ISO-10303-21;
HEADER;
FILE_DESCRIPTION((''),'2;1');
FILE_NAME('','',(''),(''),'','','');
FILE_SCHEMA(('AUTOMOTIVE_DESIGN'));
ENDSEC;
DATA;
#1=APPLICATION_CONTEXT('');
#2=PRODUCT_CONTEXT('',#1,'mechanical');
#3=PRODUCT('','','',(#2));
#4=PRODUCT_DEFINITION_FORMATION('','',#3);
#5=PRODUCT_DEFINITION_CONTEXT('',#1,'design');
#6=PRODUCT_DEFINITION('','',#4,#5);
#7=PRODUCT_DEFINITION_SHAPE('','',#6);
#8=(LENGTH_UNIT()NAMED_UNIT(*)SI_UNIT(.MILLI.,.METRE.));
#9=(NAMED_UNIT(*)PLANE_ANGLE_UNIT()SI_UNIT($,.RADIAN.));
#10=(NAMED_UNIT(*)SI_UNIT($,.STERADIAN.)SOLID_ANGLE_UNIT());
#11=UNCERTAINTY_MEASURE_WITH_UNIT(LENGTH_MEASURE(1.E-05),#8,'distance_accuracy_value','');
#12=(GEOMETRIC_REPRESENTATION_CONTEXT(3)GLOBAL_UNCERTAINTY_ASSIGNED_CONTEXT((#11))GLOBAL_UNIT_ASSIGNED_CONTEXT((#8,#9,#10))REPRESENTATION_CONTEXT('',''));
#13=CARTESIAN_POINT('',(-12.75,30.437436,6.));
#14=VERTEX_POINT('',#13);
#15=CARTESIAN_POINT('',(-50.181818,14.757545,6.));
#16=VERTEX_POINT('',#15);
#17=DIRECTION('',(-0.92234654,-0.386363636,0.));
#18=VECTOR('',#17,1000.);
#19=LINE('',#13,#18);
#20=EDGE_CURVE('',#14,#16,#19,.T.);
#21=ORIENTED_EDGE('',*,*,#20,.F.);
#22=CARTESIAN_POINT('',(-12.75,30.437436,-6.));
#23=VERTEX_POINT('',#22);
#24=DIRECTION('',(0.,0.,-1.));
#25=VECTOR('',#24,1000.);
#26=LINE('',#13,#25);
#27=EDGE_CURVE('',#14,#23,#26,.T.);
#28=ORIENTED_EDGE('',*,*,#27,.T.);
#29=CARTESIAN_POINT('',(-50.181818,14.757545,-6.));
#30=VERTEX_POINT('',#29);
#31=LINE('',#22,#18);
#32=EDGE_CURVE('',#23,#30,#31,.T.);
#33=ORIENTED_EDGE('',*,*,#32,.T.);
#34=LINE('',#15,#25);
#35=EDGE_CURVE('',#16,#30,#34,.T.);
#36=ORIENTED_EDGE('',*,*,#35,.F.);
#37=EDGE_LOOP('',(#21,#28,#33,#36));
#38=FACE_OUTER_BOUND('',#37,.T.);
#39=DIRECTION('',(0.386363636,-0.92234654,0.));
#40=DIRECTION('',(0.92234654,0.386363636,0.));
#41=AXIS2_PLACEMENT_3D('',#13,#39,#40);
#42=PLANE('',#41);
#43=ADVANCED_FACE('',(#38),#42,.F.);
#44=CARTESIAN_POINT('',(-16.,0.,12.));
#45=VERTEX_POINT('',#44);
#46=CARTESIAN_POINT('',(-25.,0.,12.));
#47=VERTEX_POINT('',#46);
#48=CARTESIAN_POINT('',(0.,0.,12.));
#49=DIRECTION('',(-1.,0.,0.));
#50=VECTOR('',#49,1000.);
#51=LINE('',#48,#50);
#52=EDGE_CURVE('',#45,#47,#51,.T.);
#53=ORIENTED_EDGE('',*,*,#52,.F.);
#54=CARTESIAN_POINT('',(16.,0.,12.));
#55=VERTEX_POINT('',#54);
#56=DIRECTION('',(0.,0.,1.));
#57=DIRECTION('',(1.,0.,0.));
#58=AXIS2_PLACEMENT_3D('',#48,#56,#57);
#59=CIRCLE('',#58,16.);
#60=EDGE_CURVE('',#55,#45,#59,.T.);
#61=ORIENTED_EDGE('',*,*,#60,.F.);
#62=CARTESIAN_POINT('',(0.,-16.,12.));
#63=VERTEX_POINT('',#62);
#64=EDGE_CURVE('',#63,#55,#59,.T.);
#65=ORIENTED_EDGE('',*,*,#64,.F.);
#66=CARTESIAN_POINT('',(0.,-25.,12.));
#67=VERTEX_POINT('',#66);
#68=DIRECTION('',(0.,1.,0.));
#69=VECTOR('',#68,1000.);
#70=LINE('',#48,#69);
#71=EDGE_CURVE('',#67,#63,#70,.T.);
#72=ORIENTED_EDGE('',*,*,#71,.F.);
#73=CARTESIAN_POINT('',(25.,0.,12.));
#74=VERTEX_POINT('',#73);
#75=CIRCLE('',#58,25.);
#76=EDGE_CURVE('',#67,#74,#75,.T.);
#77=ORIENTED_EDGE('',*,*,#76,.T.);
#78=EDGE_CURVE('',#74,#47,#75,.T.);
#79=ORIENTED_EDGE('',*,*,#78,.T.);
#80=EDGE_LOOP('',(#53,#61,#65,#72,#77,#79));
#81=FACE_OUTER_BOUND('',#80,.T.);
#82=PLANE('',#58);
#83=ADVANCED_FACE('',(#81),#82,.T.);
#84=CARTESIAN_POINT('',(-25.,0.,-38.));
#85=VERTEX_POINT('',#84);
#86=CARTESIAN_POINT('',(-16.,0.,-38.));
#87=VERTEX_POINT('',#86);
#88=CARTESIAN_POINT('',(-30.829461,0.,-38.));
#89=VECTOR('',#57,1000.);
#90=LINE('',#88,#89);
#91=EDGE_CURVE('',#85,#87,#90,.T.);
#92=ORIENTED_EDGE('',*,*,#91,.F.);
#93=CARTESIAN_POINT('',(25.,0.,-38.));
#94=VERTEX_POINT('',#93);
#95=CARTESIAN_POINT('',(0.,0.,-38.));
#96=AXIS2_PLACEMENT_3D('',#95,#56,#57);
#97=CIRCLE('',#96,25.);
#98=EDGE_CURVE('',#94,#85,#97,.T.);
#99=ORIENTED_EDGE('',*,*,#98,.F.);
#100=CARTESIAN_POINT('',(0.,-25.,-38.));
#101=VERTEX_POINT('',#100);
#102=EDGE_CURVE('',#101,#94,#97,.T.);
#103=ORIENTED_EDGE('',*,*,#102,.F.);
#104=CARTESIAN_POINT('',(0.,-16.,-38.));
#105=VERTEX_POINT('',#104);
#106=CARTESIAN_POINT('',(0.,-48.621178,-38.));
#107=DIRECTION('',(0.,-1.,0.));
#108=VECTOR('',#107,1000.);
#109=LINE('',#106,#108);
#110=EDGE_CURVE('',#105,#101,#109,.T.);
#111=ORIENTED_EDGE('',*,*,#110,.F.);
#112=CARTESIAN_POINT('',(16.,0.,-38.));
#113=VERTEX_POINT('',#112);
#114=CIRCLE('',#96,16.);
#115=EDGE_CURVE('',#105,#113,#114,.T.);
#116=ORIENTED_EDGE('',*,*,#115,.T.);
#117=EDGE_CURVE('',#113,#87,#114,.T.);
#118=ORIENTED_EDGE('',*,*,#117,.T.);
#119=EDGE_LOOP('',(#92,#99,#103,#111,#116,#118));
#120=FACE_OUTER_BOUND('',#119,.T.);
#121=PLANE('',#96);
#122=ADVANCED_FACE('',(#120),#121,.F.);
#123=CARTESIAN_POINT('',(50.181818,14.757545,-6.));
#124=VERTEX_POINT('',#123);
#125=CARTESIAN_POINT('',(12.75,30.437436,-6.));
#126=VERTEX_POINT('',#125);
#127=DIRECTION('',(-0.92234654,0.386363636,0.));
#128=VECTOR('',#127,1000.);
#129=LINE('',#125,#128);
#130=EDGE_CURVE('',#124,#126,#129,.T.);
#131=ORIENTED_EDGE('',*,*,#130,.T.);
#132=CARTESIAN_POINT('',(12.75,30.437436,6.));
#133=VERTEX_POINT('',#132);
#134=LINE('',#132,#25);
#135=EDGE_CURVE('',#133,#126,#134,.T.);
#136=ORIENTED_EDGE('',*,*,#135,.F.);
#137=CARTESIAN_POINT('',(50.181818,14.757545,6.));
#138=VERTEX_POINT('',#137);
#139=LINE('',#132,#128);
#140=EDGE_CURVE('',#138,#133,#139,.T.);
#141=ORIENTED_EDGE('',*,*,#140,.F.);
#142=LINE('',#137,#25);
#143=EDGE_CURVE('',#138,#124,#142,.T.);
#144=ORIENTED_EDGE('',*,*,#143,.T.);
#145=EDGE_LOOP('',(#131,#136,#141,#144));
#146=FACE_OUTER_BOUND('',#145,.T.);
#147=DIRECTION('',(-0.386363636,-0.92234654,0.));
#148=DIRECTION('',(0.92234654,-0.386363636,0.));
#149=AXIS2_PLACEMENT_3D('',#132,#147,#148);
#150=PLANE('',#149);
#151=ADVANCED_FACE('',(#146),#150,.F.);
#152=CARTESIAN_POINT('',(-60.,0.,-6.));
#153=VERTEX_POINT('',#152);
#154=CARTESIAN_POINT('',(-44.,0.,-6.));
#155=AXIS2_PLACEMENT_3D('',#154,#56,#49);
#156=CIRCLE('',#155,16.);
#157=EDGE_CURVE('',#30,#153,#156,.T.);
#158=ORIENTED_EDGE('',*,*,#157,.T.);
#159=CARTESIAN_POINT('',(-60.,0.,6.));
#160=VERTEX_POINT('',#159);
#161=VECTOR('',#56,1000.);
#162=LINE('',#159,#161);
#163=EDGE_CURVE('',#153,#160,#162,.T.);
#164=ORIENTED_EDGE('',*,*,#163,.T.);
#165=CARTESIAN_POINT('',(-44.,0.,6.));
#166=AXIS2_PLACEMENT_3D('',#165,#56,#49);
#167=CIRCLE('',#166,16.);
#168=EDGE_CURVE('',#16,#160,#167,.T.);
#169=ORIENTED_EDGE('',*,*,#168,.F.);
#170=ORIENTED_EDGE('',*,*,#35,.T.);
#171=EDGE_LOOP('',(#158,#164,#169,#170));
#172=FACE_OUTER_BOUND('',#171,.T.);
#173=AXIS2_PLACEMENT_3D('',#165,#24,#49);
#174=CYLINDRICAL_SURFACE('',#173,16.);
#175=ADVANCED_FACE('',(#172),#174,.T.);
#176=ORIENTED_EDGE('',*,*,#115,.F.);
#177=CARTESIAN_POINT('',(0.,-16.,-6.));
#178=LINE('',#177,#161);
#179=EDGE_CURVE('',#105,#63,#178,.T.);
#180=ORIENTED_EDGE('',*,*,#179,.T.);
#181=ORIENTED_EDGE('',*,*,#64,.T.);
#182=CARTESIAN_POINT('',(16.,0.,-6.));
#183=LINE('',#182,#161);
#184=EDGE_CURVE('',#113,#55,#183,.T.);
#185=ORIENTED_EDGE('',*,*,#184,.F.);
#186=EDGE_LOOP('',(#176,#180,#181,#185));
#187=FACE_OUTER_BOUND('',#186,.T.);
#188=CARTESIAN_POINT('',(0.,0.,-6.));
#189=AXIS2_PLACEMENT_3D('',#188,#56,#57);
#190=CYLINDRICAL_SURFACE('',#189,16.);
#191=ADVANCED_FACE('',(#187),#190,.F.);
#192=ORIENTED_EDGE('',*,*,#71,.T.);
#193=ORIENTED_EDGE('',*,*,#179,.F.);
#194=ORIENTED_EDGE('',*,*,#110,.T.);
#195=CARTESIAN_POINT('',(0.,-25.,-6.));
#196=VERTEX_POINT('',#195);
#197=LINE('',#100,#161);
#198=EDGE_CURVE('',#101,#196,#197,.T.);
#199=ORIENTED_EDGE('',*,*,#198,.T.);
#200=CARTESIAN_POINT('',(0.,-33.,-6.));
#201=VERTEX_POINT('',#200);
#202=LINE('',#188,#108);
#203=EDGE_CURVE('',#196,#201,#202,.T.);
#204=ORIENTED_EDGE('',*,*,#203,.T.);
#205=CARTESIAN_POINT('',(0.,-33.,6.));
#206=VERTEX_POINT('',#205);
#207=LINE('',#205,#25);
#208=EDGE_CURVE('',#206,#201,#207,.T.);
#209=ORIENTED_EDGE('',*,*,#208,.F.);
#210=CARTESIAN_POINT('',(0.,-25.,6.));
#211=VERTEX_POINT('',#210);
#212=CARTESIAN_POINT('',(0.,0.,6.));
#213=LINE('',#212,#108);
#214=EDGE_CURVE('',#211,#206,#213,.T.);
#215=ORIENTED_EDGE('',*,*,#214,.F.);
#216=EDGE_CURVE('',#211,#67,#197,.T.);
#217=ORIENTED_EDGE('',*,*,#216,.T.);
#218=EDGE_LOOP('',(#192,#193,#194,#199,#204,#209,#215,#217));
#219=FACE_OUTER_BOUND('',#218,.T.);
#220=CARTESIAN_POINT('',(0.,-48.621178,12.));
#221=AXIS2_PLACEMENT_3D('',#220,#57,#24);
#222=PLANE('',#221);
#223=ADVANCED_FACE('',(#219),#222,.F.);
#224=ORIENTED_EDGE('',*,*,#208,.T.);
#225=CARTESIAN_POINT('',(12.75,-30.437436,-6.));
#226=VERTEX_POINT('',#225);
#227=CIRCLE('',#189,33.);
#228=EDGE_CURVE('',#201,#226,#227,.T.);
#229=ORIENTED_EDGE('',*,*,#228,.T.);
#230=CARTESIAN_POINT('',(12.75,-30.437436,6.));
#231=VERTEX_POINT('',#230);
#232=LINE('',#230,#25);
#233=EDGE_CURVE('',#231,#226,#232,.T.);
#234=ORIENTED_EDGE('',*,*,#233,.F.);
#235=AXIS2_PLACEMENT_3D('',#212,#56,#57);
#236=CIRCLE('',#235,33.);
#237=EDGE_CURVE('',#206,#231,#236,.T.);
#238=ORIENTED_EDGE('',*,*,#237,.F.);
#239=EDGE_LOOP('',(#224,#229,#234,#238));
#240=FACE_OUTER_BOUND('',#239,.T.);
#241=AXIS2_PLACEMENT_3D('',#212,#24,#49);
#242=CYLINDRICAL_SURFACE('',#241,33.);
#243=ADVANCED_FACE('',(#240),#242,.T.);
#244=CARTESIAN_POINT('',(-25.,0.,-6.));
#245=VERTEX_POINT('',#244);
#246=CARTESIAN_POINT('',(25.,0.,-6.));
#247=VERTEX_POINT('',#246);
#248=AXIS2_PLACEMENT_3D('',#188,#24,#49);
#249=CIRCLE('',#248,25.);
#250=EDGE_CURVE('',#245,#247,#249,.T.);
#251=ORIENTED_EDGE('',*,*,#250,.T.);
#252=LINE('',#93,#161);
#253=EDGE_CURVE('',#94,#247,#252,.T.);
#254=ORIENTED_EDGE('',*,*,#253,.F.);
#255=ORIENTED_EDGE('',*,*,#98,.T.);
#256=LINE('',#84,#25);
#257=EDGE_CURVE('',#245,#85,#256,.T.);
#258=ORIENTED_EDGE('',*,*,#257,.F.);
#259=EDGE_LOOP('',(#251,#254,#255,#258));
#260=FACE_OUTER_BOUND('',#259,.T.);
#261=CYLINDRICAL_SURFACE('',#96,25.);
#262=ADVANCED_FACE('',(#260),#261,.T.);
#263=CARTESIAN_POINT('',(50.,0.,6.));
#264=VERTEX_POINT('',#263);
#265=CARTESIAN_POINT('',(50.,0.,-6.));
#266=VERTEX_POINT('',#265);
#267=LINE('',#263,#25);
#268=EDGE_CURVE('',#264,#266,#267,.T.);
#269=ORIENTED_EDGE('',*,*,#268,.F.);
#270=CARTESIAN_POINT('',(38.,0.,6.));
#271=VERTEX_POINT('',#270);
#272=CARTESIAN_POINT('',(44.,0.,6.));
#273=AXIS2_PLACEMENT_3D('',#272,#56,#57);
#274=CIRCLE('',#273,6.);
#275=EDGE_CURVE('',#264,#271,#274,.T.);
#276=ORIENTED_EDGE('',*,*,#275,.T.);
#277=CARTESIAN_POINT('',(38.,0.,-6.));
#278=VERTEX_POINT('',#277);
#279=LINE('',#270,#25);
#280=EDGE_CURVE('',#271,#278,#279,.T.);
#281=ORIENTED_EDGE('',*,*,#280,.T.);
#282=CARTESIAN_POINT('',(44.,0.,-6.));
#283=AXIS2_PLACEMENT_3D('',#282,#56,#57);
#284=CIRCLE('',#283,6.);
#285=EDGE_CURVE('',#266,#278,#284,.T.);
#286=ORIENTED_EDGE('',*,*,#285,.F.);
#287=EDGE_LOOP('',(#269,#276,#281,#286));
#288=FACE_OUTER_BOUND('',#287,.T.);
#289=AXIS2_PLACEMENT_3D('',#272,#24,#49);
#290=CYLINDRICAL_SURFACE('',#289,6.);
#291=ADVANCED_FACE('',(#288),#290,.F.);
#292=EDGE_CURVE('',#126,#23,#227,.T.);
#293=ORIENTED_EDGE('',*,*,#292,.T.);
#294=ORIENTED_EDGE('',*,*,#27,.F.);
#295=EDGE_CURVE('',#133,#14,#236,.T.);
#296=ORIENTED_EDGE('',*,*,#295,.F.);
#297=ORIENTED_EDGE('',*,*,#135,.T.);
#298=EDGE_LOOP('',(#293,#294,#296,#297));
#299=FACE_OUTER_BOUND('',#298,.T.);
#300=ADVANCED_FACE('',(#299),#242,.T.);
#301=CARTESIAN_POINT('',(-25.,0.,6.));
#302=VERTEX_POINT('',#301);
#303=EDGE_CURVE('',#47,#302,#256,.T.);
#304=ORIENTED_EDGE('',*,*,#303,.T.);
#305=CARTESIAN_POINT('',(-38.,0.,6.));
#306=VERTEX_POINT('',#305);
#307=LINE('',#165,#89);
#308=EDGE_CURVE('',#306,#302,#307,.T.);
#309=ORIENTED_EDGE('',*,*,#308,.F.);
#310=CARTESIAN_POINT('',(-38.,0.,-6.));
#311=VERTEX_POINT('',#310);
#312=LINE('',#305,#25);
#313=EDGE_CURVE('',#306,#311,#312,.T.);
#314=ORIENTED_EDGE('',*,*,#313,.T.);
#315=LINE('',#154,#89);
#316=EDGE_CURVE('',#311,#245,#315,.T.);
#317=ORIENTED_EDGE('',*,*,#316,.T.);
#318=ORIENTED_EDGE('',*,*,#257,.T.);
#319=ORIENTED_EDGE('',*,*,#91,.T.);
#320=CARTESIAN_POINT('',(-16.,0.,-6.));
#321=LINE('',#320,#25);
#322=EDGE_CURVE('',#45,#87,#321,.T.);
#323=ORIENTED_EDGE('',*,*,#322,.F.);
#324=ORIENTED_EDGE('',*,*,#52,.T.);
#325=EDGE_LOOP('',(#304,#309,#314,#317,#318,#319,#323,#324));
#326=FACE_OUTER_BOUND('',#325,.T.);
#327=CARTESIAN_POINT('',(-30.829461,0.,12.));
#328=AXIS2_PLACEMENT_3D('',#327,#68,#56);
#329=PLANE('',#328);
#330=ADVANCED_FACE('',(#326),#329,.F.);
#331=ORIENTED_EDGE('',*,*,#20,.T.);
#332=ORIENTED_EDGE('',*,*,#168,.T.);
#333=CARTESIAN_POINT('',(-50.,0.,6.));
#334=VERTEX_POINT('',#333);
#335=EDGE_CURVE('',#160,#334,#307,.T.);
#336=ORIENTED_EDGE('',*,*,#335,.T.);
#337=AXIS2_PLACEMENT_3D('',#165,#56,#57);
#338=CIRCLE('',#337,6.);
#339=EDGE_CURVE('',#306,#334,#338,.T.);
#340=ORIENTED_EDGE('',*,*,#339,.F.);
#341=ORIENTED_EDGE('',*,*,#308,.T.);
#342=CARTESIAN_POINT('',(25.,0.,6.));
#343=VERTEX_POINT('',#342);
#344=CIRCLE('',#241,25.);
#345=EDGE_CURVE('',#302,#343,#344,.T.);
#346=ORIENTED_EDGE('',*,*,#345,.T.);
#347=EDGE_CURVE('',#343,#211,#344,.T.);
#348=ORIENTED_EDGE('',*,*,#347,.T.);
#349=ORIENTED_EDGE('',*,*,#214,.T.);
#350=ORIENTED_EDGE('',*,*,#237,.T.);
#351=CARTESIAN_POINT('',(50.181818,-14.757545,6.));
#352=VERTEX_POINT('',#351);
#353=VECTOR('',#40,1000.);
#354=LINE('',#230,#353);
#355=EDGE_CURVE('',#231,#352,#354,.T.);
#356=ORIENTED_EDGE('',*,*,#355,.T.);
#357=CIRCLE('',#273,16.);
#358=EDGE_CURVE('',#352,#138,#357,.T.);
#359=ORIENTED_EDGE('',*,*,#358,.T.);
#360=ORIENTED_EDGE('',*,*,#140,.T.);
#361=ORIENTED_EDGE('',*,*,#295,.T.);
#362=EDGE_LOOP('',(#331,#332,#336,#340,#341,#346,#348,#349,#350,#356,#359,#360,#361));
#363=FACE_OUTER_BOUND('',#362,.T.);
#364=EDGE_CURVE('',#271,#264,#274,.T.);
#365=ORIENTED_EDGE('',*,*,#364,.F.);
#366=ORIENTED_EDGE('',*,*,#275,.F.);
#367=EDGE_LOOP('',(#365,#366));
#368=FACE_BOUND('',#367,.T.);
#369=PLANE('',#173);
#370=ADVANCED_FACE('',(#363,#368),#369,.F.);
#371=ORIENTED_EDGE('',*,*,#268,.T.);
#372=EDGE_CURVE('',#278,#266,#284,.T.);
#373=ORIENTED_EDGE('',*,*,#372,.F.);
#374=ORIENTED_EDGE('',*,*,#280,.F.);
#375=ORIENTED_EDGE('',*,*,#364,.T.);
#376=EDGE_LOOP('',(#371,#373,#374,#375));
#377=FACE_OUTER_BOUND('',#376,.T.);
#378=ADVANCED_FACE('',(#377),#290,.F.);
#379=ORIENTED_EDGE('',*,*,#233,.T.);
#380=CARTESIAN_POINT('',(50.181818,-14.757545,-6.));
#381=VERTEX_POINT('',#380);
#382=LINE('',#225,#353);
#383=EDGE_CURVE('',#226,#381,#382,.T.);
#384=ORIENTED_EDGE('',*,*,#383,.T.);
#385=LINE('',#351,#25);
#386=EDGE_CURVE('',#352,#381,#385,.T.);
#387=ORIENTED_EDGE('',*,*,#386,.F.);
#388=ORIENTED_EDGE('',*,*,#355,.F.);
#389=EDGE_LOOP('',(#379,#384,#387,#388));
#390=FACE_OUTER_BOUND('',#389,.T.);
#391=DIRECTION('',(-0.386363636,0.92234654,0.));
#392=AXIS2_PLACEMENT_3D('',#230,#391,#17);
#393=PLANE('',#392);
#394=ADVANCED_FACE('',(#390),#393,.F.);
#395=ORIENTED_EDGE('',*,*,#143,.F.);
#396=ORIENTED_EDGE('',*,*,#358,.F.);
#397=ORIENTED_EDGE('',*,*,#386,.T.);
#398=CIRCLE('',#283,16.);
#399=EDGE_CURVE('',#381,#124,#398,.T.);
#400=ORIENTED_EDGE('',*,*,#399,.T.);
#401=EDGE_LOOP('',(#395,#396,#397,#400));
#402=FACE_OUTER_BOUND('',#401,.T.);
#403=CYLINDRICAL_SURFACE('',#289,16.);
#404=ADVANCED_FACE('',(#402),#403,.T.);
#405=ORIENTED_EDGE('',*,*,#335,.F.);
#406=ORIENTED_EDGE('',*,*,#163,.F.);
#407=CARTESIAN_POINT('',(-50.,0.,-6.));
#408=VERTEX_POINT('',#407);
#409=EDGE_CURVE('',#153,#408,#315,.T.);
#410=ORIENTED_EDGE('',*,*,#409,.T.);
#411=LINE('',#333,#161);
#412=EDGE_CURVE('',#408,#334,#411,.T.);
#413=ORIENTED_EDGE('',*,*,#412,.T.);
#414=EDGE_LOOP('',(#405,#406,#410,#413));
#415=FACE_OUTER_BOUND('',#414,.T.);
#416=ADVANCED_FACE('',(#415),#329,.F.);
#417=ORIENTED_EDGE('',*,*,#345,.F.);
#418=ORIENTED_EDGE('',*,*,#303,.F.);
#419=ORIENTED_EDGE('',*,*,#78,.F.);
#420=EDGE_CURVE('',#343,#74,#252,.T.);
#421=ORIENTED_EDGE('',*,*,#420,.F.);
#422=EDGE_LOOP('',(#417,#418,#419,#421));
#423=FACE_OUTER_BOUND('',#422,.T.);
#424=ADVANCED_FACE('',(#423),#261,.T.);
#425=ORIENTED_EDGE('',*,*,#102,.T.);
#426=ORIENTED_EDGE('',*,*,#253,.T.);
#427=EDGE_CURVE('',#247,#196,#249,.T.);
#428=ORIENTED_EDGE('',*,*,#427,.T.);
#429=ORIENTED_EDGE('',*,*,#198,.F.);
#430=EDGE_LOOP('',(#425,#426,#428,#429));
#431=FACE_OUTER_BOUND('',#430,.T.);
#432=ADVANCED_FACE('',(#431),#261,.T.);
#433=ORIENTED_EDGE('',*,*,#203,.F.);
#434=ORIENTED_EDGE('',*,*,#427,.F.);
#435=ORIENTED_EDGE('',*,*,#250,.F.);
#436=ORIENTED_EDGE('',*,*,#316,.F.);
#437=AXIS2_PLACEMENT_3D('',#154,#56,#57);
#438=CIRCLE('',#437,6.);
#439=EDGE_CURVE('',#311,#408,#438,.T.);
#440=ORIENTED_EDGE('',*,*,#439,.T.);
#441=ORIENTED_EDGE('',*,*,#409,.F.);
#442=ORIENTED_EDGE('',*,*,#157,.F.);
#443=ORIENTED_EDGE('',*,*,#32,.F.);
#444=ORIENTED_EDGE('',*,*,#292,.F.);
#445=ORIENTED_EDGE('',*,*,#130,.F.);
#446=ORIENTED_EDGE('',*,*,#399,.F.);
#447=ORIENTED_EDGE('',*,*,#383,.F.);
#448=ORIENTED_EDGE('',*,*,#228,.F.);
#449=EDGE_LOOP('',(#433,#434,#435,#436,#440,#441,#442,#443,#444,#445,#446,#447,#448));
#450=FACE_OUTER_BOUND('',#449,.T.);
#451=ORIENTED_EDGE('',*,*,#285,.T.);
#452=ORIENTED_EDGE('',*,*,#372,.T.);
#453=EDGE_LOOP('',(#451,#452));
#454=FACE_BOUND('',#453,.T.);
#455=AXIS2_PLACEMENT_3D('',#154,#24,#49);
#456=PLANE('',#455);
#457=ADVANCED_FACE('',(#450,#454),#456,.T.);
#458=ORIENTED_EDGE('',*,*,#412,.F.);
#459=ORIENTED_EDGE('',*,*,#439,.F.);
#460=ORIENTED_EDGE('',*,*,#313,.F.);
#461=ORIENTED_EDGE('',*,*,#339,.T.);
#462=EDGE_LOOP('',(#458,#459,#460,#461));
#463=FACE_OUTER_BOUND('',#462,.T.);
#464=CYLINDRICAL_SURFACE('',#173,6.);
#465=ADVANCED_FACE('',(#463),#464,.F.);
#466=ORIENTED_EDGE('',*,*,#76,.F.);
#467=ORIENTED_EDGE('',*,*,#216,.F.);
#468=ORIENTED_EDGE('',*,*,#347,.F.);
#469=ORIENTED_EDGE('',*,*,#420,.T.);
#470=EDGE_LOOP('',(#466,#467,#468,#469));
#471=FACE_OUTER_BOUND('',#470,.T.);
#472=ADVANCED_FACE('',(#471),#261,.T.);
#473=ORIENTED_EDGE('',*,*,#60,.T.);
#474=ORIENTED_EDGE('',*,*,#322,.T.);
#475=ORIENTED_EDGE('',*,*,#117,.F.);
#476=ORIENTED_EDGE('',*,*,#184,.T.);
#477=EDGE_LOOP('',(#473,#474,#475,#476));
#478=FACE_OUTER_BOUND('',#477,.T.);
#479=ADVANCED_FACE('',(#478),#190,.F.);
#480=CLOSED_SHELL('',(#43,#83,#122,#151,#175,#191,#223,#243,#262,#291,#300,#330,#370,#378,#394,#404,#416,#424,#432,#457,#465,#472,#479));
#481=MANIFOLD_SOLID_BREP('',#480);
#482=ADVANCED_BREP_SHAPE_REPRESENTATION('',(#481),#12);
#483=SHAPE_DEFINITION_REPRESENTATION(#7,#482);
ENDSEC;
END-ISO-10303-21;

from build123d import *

# Parameters (mm, degrees)
BRACKET_PLATE_PROFILE_R  = 6
BRACKET_PLATE_12MM_DEPTH = 6
HUB_AND_BORE_CIRCLES_R   = 16
BORE_32_DEPTH            = 12
HUB_50_DEPTH             = 6
HUB_50_DEPTH_BACK        = 44
SKETCH2_3_R              = 25
SKETCH2_3_R_2            = 16
HUB_SLOT_CUT_DEPTH       = 85.787970845


with BuildPart() as part:
    # Bracket Plate Profile → Bracket Plate 12mm (new, symmetric)
    with BuildSketch(Plane.XY):
        with BuildLine():
            Line((12.75, 30.437435832), (50.181818182, 14.757544646))
            ThreePointArc((50.181818182, 14.757544646), (60, 0), (50.181818182, -14.757544646))
            Line((50.181818182, -14.757544646), (12.75, -30.437435832))
            ThreePointArc((12.75, -30.437435832), (0, -33), (-12.75, -30.437435832))
            Line((-12.75, -30.437435832), (-50.181818182, -14.757544646))
            ThreePointArc((-50.181818182, -14.757544646), (-60, 0), (-50.181818182, 14.757544646))
            Line((-50.181818182, 14.757544646), (-12.75, 30.437435832))
            ThreePointArc((-12.75, 30.437435832), (0, 33), (12.75, 30.437435832))
        make_face()
        with Locations((-44, 0)):
            Circle(BRACKET_PLATE_PROFILE_R, mode=Mode.SUBTRACT)
        with Locations((44, 0)):
            Circle(BRACKET_PLATE_PROFILE_R, mode=Mode.SUBTRACT)
    extrude(amount=BRACKET_PLATE_12MM_DEPTH, both=True)

    # Hub and Bore Circles → Bore _32 (cut)
    with BuildSketch(Plane.XY.offset(6)):
        Circle(HUB_AND_BORE_CIRCLES_R)
    extrude(amount=-BORE_32_DEPTH, mode=Mode.SUBTRACT)

    # Sketch2_3 → Hub _50 (add, two sides: drawn at the far end of the back side and taken through both)
    with BuildSketch(Plane.XY.offset(6).offset(-HUB_50_DEPTH_BACK)):
        Circle(SKETCH2_3_R)
        Circle(SKETCH2_3_R_2, mode=Mode.SUBTRACT)
    extrude(amount=HUB_50_DEPTH + HUB_50_DEPTH_BACK)

    # Hub Slot Profile → Hub Slot Cut (cut, through all)
    with BuildSketch(Plane(origin=(0, 0, -38), x_dir=(-1, 0, 0), z_dir=(0, 0, -1))):
        Polygon((0, 0), (0, -33), (0, -48.621178417), (74.791991636, 0), (30.829460929, 0), align=None)
    extrude(amount=-HUB_SLOT_CUT_DEPTH, mode=Mode.SUBTRACT)


solid = part.part
